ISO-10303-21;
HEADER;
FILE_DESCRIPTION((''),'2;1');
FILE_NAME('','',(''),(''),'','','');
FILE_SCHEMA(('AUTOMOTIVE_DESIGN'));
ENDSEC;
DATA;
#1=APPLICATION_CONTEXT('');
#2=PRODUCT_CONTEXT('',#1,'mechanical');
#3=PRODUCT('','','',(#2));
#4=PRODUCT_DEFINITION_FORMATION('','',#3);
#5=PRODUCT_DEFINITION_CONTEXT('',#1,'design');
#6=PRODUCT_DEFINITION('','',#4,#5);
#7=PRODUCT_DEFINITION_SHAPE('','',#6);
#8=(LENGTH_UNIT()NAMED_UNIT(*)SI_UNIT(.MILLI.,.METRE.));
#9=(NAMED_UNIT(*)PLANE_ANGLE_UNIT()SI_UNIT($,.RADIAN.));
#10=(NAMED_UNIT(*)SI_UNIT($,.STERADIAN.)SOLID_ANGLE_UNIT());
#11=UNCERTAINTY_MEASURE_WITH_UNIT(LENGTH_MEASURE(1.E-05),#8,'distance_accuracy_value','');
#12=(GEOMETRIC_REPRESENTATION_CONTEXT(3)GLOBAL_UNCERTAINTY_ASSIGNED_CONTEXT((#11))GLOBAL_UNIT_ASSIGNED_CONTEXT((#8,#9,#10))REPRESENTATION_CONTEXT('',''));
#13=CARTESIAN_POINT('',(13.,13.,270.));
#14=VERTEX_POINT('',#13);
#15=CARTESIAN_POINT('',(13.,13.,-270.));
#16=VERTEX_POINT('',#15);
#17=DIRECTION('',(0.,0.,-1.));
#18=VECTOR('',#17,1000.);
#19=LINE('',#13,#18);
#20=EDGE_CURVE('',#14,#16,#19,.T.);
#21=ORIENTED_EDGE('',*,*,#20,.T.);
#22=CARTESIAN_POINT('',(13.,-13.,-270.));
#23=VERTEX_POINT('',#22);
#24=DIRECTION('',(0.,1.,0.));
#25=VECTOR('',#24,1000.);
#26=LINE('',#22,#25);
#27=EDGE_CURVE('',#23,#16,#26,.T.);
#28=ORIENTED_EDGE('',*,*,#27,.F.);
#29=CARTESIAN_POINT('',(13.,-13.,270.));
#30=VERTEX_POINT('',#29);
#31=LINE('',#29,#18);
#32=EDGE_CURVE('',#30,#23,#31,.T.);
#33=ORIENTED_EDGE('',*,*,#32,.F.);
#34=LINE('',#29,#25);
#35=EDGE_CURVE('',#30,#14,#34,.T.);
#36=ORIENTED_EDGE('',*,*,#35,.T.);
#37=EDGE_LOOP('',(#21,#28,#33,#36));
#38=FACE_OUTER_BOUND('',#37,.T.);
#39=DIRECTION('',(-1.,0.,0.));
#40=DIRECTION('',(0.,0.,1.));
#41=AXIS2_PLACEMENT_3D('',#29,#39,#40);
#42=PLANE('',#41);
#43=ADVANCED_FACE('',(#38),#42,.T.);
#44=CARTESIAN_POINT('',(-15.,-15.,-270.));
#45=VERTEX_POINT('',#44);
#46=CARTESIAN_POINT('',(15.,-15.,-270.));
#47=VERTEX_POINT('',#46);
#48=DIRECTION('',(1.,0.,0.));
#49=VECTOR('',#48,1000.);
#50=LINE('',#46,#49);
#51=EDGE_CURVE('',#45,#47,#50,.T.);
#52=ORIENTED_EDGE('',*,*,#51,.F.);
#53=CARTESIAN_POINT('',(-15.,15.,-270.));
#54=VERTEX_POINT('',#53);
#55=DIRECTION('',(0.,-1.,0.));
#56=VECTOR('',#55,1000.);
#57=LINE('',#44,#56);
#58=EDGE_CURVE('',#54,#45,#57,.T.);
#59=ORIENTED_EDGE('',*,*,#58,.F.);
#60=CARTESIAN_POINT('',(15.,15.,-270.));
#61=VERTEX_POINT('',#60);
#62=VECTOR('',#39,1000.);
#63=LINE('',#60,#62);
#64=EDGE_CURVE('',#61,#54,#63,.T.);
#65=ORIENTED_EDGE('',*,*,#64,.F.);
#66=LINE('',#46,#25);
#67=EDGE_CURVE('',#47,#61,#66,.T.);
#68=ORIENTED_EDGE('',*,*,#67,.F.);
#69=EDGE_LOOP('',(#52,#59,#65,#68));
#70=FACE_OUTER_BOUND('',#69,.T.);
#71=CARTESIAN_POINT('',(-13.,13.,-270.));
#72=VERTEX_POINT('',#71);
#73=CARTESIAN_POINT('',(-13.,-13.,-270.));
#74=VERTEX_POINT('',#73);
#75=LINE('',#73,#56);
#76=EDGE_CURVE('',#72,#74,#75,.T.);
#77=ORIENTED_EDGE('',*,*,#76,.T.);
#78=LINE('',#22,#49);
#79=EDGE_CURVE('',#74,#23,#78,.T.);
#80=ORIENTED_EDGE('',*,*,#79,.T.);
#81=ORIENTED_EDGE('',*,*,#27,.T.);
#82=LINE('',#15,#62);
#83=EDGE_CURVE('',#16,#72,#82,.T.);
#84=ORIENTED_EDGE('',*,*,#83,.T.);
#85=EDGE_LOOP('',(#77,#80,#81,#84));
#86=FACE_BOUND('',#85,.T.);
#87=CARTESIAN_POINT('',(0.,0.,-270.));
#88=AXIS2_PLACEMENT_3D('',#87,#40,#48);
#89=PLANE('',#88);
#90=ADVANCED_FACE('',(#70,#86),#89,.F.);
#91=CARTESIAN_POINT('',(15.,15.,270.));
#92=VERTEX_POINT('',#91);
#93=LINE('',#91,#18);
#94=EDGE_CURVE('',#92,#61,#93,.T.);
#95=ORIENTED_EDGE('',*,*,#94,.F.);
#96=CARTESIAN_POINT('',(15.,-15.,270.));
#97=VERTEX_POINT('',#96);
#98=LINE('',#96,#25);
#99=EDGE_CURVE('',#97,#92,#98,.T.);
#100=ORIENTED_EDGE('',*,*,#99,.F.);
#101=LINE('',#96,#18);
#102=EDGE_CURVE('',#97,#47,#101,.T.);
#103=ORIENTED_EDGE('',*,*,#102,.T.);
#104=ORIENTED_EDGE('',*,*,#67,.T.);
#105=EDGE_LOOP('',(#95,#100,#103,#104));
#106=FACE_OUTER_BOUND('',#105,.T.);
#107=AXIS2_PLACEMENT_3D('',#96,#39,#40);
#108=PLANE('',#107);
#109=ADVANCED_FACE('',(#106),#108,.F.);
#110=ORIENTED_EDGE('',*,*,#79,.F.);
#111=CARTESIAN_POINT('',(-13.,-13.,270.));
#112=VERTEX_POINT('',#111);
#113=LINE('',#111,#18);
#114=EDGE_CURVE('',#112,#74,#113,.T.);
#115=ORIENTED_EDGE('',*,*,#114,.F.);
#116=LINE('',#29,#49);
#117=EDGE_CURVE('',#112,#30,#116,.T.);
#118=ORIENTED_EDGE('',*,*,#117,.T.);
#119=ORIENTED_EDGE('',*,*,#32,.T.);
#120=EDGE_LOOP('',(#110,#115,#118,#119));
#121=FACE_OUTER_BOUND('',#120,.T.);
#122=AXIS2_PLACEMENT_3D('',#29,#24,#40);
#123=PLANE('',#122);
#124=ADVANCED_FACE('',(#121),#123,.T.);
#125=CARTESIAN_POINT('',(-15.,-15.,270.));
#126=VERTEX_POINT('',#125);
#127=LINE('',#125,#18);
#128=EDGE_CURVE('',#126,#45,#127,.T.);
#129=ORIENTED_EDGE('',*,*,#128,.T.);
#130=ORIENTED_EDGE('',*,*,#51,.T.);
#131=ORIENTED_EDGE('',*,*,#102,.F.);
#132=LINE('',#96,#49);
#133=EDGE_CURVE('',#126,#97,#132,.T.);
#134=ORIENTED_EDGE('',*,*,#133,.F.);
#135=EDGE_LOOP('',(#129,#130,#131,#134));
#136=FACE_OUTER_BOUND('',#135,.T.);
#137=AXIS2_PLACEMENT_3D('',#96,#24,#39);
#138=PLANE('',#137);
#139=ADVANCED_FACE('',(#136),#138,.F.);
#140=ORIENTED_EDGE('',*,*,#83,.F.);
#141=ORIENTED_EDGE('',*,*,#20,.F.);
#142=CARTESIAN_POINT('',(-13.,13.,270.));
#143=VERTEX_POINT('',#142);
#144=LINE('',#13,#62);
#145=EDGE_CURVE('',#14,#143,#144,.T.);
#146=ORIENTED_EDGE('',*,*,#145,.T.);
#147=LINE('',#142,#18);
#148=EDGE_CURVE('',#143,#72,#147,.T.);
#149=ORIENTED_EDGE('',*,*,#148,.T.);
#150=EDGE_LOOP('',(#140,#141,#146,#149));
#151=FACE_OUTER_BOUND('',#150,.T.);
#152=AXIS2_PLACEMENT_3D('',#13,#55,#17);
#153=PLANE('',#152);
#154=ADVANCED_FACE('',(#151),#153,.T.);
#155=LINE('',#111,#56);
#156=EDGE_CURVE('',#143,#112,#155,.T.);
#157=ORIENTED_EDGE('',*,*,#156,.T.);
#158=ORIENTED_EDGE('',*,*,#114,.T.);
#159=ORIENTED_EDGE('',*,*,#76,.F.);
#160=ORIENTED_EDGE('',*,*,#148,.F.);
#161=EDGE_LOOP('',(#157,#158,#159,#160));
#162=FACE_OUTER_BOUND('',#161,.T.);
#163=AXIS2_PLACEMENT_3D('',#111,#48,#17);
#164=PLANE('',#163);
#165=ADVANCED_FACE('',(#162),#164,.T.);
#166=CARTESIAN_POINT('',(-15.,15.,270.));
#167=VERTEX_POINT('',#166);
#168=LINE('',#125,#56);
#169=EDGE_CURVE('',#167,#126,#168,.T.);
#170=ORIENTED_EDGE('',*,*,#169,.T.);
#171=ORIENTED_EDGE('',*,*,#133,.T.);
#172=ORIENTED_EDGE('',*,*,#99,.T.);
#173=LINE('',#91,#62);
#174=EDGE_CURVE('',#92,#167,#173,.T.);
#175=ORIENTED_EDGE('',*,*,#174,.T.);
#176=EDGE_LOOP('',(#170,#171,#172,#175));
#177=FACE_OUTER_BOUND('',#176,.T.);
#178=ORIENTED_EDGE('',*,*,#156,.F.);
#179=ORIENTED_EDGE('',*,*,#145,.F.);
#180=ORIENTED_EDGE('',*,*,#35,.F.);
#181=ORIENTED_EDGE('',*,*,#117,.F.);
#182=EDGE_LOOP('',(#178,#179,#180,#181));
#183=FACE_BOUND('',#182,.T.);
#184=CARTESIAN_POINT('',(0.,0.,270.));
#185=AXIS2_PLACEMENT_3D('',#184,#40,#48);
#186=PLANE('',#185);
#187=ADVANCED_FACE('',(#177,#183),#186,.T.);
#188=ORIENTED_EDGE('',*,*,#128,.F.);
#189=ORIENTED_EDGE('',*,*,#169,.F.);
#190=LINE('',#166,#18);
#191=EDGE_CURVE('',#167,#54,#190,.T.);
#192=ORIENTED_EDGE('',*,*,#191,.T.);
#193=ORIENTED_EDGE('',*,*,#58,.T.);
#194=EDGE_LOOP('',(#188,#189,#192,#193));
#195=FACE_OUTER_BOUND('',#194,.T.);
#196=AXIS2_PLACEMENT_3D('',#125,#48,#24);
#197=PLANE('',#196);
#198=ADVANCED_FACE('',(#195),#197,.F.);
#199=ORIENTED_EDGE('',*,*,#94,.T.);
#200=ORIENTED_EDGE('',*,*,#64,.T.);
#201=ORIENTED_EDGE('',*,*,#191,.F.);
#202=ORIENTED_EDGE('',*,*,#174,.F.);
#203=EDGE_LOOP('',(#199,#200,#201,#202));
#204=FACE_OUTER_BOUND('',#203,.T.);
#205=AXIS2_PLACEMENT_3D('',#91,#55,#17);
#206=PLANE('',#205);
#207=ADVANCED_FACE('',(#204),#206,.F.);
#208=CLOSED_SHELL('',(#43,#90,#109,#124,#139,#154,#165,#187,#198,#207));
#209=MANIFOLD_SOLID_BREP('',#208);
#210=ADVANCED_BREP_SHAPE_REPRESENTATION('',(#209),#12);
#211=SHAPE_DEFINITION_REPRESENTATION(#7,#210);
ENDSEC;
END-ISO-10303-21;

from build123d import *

# Parameters (mm, degrees)
SKETCH_1_W      = 30
SKETCH_1_H      = 30
SKETCH_1_W_2    = 26
SKETCH_1_H_2    = 26
EXTRUDE_1_DEPTH = 270


with BuildPart() as part:
    # 草图1 → 凸台-拉伸1 (new, symmetric)
    with BuildSketch(Plane.XY):
        Rectangle(SKETCH_1_W, SKETCH_1_H)
        Rectangle(SKETCH_1_W_2, SKETCH_1_H_2, mode=Mode.SUBTRACT)
    extrude(amount=EXTRUDE_1_DEPTH, both=True)


solid = part.part
